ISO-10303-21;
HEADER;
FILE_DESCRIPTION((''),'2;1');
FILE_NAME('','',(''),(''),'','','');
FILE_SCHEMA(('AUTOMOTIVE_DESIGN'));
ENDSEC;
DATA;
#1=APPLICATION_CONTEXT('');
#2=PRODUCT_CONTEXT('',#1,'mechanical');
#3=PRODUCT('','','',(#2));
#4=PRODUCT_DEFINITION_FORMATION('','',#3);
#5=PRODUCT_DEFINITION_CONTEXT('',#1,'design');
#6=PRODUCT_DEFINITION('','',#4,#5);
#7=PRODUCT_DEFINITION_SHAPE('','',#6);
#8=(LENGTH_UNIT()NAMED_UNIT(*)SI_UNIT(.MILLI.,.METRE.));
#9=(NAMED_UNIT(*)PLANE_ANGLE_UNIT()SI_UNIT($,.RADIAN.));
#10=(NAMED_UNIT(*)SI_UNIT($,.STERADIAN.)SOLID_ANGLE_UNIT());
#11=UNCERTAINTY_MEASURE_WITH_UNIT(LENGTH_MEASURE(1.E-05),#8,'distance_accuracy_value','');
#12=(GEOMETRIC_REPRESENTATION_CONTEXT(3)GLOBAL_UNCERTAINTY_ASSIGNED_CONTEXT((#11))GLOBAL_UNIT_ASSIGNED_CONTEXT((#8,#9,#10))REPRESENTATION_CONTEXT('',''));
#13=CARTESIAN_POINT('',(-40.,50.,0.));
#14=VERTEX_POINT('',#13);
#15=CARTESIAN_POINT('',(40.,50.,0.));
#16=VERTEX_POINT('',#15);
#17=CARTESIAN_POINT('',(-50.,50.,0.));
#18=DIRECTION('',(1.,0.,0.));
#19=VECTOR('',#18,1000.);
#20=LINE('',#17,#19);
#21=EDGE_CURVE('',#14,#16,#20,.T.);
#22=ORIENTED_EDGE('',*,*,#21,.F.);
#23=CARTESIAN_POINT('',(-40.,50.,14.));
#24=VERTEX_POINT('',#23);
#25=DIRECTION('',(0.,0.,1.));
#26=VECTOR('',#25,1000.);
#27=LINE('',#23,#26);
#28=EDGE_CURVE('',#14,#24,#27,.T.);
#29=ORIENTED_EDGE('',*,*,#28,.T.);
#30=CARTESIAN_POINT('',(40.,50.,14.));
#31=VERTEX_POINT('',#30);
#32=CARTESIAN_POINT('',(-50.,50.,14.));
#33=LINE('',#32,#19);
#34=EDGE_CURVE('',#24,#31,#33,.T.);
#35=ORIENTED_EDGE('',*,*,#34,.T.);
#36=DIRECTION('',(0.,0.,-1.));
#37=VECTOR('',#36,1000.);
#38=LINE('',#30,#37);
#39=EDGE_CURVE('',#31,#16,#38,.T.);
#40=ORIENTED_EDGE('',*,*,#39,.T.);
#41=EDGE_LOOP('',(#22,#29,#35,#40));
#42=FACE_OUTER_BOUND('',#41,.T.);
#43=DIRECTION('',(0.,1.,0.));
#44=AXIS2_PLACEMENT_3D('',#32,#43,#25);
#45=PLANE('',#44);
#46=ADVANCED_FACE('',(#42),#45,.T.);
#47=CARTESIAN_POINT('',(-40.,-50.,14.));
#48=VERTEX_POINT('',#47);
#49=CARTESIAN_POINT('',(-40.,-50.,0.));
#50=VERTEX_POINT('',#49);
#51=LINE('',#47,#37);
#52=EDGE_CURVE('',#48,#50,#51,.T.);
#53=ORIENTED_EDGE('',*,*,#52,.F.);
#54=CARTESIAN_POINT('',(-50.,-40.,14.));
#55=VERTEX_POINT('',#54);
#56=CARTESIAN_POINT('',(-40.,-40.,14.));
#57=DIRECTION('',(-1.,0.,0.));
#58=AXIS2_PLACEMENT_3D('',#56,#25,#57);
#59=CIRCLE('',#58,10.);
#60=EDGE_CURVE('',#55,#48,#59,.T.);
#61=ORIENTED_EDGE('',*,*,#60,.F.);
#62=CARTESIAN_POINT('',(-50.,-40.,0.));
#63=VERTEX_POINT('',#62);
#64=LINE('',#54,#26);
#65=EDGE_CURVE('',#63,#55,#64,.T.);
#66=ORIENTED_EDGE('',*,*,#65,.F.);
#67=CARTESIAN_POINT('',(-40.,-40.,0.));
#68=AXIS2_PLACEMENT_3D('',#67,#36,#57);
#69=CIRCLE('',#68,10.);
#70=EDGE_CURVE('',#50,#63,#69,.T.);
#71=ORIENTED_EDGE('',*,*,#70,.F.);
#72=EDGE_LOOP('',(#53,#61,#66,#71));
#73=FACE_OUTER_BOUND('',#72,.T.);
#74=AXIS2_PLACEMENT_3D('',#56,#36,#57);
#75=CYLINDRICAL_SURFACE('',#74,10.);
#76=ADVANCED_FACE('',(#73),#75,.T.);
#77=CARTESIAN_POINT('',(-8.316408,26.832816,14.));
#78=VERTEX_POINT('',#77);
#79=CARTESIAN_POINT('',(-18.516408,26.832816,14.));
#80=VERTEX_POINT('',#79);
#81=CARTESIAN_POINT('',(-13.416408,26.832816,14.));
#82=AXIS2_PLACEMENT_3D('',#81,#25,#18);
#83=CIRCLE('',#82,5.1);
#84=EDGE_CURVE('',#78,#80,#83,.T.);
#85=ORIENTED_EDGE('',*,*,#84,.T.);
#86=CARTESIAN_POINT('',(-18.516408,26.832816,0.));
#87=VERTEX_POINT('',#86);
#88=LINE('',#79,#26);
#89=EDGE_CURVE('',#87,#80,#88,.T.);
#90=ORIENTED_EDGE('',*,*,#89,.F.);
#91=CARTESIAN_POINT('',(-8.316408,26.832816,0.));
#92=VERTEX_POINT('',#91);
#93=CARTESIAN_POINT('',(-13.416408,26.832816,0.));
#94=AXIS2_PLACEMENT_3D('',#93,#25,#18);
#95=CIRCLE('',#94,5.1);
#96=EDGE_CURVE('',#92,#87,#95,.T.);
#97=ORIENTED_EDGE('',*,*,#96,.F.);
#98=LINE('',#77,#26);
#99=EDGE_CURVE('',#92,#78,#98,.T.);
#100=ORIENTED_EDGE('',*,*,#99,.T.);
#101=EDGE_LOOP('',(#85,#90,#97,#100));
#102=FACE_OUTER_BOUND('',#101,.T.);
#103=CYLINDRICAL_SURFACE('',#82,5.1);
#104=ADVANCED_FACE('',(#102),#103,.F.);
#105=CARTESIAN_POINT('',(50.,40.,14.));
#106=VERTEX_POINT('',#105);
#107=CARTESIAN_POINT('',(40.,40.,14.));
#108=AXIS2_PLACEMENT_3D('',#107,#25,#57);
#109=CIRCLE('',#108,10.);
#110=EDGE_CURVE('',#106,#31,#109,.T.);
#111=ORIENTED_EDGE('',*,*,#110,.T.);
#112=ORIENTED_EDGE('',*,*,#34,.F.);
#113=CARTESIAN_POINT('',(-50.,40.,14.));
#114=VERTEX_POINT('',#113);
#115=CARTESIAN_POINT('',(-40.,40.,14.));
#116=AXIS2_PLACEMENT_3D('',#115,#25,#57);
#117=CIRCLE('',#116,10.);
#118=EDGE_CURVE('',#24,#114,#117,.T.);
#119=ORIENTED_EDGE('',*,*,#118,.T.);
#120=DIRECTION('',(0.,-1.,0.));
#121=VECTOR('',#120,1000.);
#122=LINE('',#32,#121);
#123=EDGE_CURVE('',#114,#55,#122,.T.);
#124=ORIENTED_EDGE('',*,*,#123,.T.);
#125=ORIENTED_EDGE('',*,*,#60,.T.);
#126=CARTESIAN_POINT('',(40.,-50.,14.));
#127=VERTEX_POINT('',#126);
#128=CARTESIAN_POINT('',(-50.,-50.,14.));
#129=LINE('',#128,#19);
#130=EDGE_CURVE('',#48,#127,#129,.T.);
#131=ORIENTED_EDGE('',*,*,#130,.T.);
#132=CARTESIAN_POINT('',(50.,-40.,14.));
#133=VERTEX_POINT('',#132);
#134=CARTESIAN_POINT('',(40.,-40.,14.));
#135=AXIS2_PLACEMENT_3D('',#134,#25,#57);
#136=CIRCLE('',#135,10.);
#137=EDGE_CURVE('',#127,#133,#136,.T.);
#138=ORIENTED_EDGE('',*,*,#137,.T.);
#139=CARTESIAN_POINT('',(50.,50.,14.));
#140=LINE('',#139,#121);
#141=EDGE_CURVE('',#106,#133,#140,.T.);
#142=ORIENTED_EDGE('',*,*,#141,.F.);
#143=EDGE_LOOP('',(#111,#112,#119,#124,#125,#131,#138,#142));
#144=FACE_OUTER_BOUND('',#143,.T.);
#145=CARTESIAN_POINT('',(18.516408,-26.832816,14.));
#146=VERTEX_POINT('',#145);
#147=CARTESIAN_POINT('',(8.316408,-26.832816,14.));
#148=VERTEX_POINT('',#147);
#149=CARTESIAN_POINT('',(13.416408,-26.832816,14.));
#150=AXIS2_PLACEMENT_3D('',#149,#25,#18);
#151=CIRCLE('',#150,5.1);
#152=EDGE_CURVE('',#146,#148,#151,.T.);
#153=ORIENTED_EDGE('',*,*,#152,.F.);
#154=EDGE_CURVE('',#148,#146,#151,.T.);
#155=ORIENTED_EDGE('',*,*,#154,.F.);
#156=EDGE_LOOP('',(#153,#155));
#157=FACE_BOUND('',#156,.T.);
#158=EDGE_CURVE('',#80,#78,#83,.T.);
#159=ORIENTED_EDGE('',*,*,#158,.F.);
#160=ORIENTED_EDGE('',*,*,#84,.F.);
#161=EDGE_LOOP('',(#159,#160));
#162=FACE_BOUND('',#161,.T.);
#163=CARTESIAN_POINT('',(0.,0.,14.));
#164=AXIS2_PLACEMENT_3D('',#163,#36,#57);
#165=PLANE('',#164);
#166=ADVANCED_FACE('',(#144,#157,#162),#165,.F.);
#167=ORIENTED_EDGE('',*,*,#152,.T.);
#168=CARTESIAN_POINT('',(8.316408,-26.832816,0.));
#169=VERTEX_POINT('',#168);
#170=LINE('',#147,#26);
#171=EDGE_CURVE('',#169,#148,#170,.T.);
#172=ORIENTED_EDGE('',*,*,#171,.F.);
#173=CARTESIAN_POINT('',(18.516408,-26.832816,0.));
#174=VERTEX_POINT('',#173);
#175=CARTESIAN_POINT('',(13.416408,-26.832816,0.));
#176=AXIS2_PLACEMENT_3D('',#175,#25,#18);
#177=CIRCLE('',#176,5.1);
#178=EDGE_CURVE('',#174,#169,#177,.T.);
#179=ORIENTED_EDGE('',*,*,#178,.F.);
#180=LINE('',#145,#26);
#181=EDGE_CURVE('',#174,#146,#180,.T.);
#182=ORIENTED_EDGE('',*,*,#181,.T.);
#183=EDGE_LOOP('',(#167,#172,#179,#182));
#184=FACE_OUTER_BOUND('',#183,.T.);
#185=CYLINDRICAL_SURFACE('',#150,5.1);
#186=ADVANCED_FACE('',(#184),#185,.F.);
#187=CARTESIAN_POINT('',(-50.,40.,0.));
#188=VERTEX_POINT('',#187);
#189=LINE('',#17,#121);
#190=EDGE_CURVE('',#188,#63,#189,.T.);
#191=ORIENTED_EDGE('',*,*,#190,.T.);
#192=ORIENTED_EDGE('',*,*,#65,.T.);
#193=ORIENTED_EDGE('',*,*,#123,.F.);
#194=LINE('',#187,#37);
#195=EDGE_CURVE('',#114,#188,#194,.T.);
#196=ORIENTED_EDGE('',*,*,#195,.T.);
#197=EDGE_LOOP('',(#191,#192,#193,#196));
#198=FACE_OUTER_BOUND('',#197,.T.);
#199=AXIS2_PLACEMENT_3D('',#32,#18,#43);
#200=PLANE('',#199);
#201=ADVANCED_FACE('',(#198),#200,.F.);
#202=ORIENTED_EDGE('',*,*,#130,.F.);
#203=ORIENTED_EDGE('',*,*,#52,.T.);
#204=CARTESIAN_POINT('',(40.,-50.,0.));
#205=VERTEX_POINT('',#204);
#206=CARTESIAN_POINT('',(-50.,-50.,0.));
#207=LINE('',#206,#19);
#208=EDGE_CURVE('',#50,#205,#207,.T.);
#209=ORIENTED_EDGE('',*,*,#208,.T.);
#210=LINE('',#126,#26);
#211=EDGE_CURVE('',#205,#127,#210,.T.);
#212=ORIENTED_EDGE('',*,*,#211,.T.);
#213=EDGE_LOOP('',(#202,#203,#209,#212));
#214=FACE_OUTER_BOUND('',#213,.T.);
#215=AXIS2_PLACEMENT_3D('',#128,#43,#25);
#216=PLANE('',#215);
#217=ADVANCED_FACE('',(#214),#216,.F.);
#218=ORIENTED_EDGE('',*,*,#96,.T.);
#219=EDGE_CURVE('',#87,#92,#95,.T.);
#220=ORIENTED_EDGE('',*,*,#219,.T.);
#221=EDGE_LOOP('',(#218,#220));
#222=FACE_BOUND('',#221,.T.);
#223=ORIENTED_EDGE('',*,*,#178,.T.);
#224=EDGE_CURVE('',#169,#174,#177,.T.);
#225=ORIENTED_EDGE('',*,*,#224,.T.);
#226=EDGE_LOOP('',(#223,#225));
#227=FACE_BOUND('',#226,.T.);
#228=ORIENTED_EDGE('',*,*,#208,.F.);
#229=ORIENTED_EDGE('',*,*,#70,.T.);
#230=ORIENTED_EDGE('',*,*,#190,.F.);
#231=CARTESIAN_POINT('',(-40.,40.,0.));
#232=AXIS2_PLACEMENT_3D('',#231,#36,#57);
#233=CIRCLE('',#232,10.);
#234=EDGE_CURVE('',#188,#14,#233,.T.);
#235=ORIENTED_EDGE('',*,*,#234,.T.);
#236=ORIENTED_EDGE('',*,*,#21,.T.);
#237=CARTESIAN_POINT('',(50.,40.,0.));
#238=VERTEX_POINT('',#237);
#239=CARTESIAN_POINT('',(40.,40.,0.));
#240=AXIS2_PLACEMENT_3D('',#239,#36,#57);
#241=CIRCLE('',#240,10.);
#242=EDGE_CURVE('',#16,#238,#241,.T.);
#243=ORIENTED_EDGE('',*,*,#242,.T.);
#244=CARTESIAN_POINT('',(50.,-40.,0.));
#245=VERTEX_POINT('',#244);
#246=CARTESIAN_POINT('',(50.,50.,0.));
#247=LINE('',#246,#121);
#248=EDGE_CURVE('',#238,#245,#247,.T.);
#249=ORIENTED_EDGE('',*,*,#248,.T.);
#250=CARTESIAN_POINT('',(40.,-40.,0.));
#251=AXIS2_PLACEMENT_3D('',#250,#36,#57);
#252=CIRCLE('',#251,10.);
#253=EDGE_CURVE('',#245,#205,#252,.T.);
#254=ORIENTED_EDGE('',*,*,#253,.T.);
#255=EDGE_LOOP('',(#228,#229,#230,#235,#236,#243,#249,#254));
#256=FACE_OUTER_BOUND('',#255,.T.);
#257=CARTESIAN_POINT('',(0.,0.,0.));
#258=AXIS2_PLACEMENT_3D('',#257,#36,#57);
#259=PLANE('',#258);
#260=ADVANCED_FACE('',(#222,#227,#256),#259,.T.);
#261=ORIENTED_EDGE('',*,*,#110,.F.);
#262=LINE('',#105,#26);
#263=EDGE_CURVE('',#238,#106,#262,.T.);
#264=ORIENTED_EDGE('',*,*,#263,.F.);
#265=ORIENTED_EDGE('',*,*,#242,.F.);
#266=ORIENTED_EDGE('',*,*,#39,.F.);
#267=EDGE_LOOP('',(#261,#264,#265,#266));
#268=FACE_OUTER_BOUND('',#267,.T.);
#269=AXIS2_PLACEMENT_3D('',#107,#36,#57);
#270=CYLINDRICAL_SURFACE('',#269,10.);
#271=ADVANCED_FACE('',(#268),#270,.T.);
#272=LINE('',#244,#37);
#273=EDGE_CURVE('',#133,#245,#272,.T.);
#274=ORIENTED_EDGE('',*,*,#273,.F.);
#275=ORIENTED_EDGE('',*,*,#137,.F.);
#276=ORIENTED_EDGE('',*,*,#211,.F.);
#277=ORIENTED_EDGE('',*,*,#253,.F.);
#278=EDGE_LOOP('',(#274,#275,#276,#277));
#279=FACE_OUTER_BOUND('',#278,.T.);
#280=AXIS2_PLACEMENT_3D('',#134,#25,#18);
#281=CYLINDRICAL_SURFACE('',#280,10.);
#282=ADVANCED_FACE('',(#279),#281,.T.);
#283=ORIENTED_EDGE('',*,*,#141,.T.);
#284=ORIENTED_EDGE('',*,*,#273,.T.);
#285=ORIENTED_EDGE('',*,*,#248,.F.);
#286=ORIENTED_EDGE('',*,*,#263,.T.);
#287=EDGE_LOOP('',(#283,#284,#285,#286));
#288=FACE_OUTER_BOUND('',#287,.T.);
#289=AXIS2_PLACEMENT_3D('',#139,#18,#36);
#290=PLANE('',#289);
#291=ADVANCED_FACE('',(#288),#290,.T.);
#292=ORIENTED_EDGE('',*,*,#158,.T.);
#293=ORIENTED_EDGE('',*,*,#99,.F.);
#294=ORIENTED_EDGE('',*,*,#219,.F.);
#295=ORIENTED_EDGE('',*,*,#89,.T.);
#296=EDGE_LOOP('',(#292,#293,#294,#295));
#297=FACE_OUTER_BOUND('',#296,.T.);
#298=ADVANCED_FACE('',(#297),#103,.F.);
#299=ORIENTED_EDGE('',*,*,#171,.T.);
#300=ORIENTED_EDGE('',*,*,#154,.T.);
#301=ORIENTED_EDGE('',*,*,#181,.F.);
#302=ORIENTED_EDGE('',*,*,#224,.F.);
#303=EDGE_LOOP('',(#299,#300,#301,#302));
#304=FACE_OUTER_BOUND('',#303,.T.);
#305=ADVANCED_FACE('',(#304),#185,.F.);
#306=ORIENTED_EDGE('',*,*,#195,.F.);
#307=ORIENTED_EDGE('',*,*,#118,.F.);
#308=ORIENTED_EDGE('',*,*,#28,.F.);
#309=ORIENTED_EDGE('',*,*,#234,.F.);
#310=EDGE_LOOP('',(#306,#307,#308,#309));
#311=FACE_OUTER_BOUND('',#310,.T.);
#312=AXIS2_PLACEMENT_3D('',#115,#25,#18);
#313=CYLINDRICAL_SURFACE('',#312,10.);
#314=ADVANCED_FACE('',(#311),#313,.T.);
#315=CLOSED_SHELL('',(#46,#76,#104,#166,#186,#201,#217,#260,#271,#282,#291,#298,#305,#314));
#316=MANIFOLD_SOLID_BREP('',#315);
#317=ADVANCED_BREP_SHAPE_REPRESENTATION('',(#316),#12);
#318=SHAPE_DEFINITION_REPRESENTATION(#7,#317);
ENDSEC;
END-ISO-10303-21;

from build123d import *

# Parameters (mm, degrees)
SKETCH_1_W          = 100
SKETCH_1_H          = 100
EXTRUDE_1_DEPTH     = 14
HOLE_WIZARD_M12_1_D = 10.2
FILLET_1_R          = 10


with BuildPart() as part:
    # 草图1 → 凸台-拉伸1 (new body)
    with BuildSketch(Plane.XY):
        Rectangle(SKETCH_1_W, SKETCH_1_H)
    extrude(amount=EXTRUDE_1_DEPTH)

    # M12 螺纹孔1 (through all)
    with Locations(Plane(origin=(13.416407865, -26.83281573, 14), x_dir=(1, 0, 0), z_dir=(0, 0, 1))):
        with Locations((0, 0), (-26.83281573, 53.66563146)):
            Hole(HOLE_WIZARD_M12_1_D / 2)

    # 圆角1
    fillet_1_edges = [part.edges().sort_by_distance(p)[0] for p in [
        (-50, 50, 7),
        (-50, -50, 7),
        (50, -50, 7),
        (50, 50, 7),
    ]]
    fillet(fillet_1_edges, radius=FILLET_1_R)


solid = part.part
